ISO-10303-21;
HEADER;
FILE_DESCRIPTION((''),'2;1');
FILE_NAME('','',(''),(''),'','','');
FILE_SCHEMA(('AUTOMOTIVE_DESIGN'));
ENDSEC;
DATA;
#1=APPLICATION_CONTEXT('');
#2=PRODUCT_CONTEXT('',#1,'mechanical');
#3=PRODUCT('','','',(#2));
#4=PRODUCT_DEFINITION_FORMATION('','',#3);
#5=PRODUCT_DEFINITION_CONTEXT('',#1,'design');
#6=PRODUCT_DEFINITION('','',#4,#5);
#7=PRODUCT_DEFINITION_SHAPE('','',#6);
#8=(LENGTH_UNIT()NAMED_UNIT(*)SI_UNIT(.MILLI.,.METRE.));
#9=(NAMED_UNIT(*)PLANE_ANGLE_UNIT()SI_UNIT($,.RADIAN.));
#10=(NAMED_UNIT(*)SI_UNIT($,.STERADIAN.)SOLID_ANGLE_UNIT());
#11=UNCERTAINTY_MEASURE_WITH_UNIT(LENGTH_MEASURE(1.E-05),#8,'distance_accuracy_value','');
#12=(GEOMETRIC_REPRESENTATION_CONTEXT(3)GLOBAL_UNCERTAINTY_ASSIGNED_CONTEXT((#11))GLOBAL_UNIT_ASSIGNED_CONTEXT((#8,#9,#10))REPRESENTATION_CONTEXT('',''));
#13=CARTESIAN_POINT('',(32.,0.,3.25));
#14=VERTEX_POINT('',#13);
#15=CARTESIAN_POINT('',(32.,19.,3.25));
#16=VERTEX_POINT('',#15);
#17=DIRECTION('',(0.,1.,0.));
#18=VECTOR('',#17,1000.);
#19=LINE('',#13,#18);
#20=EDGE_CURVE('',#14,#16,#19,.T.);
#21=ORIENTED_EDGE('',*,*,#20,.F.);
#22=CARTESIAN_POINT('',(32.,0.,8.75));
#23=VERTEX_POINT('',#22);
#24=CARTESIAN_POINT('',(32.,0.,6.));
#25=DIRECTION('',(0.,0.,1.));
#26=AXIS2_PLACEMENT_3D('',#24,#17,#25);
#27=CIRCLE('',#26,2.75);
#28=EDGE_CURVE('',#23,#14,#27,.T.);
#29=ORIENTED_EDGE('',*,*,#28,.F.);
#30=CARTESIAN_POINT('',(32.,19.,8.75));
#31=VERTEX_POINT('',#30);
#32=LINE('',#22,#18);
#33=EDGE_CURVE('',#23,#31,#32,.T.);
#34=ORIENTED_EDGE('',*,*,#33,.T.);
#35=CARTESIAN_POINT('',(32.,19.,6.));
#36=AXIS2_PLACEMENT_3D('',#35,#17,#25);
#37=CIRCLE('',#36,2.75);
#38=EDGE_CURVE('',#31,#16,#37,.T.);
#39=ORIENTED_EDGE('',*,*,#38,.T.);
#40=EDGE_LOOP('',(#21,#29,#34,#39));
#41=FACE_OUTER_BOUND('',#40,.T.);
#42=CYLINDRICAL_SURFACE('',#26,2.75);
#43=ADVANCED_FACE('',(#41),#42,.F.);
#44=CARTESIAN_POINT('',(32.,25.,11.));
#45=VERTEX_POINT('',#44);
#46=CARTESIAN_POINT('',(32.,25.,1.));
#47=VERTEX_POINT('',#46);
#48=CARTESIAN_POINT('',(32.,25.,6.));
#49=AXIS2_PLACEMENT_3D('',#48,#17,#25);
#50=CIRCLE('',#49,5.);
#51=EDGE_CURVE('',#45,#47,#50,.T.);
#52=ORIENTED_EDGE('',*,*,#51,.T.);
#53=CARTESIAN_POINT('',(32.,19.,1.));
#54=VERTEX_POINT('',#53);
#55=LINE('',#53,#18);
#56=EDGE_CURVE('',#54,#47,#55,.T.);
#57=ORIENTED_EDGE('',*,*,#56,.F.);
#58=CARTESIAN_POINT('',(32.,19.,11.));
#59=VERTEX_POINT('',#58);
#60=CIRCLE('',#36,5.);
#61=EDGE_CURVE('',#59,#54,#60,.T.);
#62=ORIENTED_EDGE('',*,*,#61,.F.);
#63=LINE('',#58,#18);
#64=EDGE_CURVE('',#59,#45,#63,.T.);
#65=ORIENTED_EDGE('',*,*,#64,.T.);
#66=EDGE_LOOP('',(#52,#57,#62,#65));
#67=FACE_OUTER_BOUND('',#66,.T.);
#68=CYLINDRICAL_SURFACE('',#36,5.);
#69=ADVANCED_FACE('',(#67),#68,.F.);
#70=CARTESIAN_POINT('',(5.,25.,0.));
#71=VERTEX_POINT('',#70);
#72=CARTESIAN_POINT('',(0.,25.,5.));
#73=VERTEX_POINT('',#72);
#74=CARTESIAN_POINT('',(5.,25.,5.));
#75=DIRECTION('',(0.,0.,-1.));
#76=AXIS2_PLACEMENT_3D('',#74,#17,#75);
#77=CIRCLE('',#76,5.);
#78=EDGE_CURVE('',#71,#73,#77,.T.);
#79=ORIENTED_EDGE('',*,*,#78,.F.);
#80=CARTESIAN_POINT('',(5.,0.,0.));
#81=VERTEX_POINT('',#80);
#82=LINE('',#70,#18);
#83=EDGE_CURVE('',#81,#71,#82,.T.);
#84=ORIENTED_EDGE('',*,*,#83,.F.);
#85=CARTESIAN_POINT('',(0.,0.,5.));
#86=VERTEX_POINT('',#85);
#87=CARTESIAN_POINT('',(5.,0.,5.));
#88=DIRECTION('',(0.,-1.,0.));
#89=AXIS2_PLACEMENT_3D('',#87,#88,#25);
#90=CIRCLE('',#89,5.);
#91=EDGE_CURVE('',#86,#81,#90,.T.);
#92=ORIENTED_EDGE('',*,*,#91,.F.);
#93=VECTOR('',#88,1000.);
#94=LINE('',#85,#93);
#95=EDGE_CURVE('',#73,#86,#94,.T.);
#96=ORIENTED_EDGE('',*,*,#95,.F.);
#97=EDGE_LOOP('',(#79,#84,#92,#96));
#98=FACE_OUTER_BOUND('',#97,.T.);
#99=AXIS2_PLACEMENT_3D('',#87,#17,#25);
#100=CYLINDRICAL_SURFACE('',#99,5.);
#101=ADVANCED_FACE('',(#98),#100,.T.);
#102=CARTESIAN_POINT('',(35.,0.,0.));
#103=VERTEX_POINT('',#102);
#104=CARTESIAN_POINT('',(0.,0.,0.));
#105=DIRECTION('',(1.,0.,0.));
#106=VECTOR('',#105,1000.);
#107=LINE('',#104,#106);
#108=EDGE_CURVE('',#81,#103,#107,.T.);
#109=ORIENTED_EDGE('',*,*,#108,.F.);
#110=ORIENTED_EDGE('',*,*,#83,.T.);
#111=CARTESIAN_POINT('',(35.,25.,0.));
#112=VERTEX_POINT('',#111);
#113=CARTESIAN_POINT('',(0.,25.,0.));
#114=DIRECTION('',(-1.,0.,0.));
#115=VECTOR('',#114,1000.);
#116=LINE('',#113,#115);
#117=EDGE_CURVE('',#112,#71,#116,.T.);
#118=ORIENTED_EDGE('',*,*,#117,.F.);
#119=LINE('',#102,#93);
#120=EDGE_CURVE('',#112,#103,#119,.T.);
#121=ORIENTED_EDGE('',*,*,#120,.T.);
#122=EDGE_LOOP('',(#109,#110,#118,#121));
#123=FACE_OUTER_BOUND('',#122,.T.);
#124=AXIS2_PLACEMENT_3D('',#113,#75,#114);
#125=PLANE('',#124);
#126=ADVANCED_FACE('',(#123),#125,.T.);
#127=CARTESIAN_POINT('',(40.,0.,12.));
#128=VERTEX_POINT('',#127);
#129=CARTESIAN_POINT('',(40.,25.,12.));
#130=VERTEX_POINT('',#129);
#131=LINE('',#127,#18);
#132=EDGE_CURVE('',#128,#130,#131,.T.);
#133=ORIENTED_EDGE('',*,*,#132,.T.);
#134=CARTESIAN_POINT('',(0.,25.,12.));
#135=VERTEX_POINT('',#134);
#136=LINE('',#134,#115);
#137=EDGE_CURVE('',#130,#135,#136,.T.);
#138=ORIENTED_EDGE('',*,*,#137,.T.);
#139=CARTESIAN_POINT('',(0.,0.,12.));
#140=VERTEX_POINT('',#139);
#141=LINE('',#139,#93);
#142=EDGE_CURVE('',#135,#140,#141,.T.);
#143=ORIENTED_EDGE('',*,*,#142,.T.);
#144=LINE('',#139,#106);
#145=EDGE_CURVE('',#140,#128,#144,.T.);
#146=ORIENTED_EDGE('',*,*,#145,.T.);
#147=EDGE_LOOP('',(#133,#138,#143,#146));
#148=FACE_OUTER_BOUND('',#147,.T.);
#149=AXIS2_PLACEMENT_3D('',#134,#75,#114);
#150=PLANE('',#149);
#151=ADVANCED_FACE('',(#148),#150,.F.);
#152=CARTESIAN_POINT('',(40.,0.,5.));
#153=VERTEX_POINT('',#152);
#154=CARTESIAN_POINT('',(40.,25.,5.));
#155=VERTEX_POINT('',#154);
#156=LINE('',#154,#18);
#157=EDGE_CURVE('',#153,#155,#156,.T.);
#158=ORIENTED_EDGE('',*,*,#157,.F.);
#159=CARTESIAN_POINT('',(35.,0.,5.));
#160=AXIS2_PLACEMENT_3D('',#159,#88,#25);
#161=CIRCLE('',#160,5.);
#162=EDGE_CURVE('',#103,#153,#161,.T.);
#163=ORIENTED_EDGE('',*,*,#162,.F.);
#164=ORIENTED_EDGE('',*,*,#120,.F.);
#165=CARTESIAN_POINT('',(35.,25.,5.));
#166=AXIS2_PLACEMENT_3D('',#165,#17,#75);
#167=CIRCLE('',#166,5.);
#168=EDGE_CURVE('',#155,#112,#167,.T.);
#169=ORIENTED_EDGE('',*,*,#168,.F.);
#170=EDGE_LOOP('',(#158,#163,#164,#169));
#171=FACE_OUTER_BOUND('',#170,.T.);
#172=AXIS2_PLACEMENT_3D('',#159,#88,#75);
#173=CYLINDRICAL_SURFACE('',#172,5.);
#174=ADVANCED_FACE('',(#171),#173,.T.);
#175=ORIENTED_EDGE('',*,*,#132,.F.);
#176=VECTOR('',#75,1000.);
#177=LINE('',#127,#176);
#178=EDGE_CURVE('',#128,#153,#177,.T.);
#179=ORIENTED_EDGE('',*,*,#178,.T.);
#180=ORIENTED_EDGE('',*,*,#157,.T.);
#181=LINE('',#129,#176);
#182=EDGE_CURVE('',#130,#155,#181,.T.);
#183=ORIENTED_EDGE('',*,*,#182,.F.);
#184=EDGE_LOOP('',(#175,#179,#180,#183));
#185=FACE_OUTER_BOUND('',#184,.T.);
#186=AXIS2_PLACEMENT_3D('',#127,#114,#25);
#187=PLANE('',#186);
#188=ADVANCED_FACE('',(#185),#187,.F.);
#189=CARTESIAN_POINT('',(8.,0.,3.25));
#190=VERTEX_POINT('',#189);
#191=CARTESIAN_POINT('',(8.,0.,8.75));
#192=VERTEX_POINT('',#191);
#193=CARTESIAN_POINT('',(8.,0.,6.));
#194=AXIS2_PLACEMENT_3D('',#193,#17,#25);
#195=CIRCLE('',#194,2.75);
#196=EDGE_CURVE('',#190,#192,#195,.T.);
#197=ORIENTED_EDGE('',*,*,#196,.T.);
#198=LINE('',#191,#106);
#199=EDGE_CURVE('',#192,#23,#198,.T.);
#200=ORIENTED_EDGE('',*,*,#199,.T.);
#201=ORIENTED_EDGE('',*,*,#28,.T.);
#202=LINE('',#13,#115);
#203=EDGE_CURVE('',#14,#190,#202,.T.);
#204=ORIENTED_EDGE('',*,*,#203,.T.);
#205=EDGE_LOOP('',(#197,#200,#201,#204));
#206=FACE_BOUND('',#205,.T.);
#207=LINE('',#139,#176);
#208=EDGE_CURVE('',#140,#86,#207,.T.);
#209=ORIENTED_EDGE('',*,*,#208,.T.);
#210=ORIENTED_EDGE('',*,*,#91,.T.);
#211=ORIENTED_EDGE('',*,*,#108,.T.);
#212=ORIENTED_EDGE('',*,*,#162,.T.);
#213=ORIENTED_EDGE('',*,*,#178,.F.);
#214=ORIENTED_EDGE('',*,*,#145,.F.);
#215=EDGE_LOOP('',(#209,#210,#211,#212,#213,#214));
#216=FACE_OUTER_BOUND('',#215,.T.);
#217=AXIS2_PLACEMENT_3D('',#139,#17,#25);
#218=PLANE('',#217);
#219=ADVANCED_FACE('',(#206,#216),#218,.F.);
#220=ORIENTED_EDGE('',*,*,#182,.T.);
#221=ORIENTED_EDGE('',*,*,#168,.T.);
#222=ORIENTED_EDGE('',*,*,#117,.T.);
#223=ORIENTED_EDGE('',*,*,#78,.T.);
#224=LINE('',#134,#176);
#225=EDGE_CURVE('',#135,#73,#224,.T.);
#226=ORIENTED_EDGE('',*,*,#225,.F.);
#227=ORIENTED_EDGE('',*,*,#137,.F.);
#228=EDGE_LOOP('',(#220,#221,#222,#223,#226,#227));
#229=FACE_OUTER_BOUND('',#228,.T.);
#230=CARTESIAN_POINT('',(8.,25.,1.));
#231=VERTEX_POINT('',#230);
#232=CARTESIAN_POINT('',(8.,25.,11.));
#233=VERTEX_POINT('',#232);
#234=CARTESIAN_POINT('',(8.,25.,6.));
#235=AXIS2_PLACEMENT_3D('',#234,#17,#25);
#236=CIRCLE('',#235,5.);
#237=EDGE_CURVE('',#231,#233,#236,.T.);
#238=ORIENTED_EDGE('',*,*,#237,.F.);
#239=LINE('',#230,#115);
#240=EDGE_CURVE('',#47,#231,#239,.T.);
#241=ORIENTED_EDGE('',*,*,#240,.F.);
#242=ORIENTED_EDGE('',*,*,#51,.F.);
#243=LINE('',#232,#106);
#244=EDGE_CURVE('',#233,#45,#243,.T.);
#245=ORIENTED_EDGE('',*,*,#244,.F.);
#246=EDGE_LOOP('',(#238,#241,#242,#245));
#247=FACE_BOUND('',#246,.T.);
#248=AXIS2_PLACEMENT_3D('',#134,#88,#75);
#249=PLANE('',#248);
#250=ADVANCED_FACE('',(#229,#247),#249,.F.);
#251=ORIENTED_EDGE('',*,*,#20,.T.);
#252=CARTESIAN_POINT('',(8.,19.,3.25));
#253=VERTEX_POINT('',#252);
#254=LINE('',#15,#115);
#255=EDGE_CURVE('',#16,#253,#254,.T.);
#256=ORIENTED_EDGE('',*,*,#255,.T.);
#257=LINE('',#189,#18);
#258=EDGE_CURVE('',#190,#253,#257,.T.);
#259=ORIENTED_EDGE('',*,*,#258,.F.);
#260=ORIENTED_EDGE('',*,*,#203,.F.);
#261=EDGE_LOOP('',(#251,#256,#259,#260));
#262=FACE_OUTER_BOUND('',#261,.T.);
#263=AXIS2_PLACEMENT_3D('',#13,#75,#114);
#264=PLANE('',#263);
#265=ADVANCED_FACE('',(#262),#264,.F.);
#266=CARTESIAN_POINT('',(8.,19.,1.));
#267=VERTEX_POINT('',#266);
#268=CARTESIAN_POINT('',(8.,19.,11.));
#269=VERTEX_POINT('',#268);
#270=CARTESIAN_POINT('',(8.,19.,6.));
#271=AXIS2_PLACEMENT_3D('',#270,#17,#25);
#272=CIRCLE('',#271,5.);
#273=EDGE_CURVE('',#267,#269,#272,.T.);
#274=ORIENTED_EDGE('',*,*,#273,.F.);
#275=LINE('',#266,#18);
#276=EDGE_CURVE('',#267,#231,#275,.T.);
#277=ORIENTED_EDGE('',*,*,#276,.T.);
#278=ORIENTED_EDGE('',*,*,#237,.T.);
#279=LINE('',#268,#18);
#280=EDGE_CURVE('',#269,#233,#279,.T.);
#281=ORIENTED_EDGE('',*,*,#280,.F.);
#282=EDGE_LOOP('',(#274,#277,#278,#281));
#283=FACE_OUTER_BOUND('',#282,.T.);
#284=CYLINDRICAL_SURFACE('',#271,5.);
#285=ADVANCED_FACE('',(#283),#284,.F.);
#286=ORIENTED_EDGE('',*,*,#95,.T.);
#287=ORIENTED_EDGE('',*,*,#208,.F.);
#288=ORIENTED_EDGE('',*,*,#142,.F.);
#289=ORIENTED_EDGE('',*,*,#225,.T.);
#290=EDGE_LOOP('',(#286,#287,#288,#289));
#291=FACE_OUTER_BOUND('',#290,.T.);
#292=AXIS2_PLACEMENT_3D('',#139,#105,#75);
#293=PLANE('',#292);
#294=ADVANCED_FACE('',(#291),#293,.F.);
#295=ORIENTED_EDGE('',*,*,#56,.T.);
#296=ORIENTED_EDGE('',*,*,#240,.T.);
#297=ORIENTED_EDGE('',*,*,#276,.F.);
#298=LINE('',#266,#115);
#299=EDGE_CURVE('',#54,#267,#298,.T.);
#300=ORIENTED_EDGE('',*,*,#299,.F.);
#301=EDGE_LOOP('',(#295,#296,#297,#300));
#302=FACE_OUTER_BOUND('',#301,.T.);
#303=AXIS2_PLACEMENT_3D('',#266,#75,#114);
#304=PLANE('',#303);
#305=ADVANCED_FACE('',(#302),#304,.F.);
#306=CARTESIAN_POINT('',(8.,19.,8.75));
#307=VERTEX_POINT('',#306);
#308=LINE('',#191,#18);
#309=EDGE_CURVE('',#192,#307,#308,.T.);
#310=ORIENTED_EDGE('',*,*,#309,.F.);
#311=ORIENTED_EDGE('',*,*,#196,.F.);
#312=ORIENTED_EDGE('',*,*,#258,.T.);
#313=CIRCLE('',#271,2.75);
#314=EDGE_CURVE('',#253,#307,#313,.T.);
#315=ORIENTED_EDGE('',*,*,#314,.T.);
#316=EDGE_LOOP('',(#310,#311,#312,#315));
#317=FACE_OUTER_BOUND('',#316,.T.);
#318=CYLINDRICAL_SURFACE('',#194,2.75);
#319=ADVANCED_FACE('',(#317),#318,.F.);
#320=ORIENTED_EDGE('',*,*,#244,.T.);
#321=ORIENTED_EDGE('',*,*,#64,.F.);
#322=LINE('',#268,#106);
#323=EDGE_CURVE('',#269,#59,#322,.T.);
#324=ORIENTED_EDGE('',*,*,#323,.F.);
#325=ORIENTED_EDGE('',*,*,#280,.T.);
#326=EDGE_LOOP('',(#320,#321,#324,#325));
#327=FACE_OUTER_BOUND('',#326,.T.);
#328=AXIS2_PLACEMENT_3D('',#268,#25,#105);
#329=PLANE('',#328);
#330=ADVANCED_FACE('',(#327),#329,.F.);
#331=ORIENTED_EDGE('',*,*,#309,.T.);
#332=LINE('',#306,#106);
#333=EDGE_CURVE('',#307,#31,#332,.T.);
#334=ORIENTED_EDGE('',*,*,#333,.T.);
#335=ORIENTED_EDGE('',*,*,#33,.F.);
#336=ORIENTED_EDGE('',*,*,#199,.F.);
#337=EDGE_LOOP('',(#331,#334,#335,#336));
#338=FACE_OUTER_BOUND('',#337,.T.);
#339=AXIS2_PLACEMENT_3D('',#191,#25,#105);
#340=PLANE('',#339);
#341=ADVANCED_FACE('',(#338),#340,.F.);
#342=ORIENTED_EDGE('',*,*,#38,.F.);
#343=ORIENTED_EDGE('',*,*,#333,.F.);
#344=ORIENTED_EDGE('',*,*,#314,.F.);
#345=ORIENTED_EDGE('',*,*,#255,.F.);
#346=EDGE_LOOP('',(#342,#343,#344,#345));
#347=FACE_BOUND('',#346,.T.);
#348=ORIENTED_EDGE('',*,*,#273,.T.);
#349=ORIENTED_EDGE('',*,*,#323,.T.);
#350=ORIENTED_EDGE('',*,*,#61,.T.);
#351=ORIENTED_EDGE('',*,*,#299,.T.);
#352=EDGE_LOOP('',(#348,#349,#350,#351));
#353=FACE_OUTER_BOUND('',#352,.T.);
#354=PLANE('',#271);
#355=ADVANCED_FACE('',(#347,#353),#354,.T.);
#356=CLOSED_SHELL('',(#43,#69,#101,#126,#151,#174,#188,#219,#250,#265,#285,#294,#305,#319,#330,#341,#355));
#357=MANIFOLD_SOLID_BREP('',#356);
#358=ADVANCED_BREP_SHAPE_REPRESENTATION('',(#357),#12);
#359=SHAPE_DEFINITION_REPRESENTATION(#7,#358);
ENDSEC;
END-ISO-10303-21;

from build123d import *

# Parameters (mm, degrees)
SKETCH_1_W          = 40
SKETCH_1_H          = 25
EXTRUDE_1_DEPTH     = 12
CUT_EXTRUDE_1_DEPTH = 6
CUT_EXTRUDE_2_DEPTH = 19
FILLET_1_R          = 5


with BuildPart() as part:
    # 草图1 → 凸台-拉伸1 (new body)
    with BuildSketch(Plane.XY):
        with Locations((20, 12.5)):
            Rectangle(SKETCH_1_W, SKETCH_1_H)
    extrude(amount=EXTRUDE_1_DEPTH)

    # 草图4 → 切除-拉伸1 (cut)
    with BuildSketch(Plane(origin=(0, 25, 0), x_dir=(1, 0, 0), z_dir=(0, 1, 0))):
        with BuildLine():
            Line((8, -1), (32, -1))
            ThreePointArc((32, -1), (37, -6), (32, -11))
            Line((32, -11), (8, -11))
            ThreePointArc((8, -11), (3, -6), (8, -1))
        make_face()
    extrude(amount=-CUT_EXTRUDE_1_DEPTH, mode=Mode.SUBTRACT)

    # 草图5 → 切除-拉伸2 (cut)
    with BuildSketch(Plane(origin=(0, 19, 0), x_dir=(1, 0, 0), z_dir=(0, 1, 0))):
        with BuildLine():
            Line((8, -8.75), (32, -8.75))
            ThreePointArc((32, -8.75), (34.75, -6), (32, -3.25))
            Line((32, -3.25), (8, -3.25))
            ThreePointArc((8, -3.25), (5.25, -6), (8, -8.75))
        make_face()
    extrude(amount=-CUT_EXTRUDE_2_DEPTH, mode=Mode.SUBTRACT)

    # 圆角1
    fillet_1_edges = [part.edges().sort_by_distance(p)[0] for p in [
        (40, 12.5, 0),
        (0, 12.5, 0),
    ]]
    fillet(fillet_1_edges, radius=FILLET_1_R)


solid = part.part
